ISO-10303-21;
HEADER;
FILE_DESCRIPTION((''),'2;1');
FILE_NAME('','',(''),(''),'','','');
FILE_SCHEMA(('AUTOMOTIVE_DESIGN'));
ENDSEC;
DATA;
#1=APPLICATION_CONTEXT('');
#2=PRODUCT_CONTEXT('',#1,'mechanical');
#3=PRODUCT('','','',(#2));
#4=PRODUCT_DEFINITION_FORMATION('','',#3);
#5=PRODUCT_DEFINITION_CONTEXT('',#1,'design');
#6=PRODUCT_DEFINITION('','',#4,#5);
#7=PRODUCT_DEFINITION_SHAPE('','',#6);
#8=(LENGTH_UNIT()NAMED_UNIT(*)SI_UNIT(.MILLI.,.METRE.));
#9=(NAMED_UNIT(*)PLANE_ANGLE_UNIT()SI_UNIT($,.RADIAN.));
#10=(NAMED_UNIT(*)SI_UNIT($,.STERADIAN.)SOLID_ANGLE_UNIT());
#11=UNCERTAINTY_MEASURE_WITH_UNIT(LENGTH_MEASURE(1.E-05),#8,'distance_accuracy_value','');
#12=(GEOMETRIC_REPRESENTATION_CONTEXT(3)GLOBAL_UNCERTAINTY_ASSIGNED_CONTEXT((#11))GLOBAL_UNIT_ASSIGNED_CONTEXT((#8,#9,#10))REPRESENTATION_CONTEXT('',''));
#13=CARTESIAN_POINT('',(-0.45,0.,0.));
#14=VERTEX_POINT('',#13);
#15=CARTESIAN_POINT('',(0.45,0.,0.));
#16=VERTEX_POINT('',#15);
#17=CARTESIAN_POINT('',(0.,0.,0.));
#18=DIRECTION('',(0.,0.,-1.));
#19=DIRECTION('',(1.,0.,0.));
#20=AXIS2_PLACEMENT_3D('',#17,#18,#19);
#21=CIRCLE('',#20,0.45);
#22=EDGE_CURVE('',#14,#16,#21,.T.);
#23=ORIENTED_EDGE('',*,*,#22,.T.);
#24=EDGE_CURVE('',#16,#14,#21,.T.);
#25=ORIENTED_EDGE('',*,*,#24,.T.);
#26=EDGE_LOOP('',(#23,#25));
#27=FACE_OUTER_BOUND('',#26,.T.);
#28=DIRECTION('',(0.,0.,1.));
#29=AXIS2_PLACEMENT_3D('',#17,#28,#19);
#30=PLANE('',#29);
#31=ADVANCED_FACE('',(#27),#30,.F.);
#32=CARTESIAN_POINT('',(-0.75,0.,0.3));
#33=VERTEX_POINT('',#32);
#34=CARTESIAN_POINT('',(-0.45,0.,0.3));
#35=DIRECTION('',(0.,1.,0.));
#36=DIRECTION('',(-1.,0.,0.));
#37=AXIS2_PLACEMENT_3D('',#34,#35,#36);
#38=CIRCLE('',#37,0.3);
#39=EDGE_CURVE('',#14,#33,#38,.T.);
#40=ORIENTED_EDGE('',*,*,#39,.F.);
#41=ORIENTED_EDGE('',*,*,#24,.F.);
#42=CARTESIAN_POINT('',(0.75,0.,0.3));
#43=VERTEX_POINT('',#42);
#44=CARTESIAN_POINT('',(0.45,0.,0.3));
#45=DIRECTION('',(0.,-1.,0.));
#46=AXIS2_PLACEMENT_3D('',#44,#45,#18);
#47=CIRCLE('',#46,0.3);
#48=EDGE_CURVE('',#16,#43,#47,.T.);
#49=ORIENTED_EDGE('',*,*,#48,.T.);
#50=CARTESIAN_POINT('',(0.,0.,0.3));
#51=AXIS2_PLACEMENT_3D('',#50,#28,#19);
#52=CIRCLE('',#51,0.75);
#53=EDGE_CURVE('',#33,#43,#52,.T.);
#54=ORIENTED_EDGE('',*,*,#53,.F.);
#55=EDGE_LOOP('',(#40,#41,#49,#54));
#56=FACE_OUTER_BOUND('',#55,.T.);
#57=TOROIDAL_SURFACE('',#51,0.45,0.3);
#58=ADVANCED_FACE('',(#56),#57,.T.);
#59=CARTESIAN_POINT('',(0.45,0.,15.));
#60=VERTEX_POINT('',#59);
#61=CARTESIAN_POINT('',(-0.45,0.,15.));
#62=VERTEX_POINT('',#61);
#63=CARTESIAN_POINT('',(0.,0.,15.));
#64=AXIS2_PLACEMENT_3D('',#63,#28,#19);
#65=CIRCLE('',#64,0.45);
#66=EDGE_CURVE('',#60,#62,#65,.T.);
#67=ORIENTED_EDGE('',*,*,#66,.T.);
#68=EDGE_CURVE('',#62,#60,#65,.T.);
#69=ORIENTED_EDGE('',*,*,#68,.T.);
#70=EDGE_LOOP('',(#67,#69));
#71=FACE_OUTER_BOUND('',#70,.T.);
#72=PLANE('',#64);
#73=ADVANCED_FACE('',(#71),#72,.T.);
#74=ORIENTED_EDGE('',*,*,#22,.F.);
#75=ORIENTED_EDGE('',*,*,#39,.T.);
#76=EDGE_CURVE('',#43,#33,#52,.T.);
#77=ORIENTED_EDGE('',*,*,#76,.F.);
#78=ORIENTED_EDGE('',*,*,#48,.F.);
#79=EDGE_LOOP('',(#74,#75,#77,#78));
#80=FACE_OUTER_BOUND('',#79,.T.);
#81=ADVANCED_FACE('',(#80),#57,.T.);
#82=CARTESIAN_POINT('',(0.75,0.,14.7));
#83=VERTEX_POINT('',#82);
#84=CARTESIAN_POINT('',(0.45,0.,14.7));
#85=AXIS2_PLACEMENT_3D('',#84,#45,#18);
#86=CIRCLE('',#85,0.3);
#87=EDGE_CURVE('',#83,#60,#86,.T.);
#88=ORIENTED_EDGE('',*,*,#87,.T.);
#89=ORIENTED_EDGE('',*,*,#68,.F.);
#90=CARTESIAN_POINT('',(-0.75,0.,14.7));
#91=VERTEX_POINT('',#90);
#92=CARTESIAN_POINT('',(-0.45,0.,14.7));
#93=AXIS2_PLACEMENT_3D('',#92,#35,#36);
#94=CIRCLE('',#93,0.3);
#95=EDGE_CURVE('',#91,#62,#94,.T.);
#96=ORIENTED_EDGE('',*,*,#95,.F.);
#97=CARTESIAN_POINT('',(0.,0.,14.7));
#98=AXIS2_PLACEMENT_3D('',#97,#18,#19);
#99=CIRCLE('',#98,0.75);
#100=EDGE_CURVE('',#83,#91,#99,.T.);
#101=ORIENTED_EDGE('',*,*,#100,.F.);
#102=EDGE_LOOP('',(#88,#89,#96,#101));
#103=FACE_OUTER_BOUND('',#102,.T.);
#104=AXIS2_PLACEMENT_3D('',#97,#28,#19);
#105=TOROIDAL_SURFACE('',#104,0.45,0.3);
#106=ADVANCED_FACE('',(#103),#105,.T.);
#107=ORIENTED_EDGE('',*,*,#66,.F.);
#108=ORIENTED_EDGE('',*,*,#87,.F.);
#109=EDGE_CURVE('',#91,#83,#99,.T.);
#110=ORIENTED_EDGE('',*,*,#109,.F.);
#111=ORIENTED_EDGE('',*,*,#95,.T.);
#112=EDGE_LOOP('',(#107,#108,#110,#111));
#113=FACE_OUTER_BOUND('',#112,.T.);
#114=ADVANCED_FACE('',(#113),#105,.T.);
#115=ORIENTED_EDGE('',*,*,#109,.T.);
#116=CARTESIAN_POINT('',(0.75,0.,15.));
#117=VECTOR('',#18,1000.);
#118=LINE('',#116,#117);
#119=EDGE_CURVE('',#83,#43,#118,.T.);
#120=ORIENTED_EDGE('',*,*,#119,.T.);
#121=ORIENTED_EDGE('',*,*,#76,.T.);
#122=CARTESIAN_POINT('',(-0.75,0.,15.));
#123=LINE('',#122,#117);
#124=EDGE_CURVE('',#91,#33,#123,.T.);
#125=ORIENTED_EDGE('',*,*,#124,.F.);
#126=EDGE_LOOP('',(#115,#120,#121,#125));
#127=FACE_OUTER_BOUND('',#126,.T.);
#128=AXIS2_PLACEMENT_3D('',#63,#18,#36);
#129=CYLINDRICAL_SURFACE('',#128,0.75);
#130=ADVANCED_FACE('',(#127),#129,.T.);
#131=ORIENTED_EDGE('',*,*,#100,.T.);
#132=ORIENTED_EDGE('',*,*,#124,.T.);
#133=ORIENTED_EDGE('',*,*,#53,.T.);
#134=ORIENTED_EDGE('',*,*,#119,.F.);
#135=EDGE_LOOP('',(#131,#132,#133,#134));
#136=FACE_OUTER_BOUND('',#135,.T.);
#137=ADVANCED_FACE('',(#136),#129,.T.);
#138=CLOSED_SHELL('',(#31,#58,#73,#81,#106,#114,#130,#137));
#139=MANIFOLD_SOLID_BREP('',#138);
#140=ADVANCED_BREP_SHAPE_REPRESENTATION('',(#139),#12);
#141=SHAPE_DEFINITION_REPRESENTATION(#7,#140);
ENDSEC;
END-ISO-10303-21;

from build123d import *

# Parameters (mm, degrees)
SKETCH1_R           = 0.75
BOSS_EXTRUDE1_DEPTH = 15
FILLET1_R           = 0.3


with BuildPart() as part:
    # Sketch1 → Boss-Extrude1 (new body)
    with BuildSketch(Plane.XY):
        Circle(SKETCH1_R)
    extrude(amount=BOSS_EXTRUDE1_DEPTH)

    # Fillet1
    fillet1_edges = [part.edges().sort_by_distance(p)[0] for p in [
        (-0.75, 0, 0),
        (-0.75, 0, 15),
    ]]
    fillet(fillet1_edges, radius=FILLET1_R)


solid = part.part
